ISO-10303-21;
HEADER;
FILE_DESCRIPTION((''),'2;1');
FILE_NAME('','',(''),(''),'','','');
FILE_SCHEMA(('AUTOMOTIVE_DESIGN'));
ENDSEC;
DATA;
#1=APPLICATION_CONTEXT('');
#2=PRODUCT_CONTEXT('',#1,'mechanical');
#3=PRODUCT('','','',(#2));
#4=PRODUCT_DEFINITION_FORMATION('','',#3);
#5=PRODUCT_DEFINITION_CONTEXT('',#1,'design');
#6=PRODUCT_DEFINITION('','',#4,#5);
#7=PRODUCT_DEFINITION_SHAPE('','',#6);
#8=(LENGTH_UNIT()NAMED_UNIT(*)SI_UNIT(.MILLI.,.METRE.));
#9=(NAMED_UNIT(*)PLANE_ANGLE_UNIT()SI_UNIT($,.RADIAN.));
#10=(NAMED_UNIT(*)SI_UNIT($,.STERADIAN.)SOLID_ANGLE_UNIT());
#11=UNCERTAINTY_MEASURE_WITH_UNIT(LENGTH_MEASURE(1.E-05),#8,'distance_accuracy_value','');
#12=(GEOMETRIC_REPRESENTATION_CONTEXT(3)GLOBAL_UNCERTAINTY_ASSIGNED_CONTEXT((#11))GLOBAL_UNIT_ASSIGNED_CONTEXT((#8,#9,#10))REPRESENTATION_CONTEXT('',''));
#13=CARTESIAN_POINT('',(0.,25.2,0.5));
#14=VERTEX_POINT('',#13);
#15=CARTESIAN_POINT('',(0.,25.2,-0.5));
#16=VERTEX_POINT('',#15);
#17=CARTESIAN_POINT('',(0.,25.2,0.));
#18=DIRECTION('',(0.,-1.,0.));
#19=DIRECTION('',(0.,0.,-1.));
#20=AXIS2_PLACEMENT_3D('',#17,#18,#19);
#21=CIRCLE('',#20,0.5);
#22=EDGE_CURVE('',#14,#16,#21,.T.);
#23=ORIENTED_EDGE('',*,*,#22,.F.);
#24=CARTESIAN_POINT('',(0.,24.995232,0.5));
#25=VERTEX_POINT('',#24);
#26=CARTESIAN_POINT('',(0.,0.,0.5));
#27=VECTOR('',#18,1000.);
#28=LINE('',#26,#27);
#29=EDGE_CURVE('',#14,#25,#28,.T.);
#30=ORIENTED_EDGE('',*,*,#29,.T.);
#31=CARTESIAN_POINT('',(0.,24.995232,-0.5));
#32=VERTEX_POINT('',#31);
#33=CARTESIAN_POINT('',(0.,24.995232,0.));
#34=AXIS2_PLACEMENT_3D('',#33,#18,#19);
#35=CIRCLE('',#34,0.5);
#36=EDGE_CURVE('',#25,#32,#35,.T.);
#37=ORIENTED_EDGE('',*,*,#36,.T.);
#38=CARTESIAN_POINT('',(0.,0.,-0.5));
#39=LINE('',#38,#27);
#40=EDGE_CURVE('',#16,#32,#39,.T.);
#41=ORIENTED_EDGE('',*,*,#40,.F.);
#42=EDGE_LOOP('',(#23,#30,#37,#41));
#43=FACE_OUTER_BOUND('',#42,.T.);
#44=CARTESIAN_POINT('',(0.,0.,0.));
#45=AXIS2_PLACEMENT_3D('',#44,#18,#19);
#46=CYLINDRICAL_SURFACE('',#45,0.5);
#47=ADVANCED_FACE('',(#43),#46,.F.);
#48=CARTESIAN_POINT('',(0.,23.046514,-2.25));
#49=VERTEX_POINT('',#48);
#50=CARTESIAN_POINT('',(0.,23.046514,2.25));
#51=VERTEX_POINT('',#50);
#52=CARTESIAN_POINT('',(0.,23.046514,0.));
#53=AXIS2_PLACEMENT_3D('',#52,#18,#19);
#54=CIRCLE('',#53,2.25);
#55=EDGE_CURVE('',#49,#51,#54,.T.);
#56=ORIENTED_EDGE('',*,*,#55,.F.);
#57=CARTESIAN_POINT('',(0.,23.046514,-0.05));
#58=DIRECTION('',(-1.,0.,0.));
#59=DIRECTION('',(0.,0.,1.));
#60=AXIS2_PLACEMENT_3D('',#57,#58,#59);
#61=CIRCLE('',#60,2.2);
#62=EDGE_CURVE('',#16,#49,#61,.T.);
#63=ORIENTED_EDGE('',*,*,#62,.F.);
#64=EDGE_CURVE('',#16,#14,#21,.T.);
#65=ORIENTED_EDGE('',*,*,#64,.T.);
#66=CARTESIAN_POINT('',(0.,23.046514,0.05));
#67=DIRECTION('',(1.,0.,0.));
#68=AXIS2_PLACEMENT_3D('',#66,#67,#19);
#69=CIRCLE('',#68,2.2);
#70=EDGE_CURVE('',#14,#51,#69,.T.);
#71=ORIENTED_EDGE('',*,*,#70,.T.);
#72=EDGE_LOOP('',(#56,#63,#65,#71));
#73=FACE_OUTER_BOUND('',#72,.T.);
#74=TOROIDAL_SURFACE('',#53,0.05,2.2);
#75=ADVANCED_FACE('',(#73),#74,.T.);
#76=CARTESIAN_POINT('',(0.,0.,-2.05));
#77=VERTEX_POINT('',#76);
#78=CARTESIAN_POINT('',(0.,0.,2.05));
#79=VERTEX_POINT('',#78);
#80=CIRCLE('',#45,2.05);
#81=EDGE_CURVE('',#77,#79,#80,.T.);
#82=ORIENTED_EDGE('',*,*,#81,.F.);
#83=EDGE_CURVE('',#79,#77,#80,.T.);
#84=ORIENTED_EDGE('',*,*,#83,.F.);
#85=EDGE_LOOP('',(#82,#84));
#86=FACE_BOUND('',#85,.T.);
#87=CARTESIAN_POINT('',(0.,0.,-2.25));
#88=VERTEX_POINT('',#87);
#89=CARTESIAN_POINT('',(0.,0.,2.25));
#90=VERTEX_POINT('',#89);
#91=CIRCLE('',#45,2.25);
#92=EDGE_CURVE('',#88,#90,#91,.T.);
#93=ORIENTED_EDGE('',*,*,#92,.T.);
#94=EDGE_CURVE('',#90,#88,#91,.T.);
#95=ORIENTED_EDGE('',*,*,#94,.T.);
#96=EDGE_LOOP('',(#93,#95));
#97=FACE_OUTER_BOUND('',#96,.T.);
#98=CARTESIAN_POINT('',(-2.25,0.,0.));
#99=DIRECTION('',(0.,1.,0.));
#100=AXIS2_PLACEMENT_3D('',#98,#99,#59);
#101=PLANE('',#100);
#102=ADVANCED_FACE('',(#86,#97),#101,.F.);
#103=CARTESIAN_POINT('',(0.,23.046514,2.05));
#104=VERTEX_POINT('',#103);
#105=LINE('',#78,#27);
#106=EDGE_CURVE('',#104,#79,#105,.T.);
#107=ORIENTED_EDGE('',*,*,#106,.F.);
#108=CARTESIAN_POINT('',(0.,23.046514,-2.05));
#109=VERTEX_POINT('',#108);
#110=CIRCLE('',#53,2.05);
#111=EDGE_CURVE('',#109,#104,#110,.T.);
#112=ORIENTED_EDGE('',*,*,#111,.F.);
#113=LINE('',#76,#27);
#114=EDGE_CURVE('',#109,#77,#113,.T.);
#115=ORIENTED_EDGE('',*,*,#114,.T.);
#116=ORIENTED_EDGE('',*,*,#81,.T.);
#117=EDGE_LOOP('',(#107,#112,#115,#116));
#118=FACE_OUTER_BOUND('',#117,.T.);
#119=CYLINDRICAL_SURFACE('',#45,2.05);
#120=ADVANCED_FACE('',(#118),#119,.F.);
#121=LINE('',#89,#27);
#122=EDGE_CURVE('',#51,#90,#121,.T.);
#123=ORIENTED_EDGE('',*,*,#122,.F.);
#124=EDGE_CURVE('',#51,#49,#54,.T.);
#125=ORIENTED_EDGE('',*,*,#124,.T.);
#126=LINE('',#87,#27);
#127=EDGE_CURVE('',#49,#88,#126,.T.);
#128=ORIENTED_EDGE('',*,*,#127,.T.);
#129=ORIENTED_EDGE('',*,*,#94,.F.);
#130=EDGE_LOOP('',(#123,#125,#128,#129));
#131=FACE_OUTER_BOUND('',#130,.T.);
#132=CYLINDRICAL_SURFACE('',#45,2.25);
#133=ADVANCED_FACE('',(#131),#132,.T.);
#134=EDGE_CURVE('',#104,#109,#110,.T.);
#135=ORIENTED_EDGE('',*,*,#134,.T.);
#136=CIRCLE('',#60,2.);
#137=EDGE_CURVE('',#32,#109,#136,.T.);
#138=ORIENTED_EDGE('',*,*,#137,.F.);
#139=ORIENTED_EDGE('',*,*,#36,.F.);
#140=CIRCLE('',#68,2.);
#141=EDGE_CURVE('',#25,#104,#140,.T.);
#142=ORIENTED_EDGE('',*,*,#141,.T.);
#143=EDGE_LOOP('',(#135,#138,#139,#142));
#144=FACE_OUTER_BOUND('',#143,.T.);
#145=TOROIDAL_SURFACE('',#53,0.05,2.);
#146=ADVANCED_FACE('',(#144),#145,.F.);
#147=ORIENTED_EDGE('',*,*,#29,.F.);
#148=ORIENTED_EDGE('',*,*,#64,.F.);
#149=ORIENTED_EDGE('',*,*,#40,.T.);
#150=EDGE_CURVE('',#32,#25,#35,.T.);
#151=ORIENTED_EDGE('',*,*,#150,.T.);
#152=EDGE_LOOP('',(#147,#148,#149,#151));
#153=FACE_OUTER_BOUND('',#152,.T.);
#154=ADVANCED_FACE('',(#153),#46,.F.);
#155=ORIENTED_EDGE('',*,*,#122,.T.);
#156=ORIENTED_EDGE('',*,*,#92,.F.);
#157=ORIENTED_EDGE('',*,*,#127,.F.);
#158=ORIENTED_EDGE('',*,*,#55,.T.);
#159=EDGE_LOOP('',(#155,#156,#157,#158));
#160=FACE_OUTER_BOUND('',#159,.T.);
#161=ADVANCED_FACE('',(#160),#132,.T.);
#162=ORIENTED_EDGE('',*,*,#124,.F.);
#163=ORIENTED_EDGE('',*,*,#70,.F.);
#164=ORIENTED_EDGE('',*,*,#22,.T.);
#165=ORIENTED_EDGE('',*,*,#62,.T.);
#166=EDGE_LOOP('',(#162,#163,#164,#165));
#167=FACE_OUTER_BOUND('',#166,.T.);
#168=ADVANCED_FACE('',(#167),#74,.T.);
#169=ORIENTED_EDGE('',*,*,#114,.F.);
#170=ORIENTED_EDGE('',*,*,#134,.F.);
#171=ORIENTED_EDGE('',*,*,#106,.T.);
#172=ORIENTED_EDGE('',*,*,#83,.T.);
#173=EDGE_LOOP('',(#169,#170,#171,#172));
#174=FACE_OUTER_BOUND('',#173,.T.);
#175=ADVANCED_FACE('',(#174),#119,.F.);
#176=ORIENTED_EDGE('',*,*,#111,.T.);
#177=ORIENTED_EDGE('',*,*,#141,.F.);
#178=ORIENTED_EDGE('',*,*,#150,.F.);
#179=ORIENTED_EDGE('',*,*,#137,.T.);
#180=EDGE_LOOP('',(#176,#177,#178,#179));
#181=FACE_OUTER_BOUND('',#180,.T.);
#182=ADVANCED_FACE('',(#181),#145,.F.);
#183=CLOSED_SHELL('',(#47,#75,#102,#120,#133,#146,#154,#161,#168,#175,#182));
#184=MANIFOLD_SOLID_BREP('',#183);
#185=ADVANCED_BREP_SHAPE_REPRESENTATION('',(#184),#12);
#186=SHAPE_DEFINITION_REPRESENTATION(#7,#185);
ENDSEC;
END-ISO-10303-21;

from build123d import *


with BuildPart() as part:
    # Sketch1 → Revolve1 (revolve)
    with BuildSketch(Plane.XY, mode=Mode.PRIVATE) as revolve1_sk:
        with BuildLine():
            Line((-2.25, 0), (-2.25, 23.046514453))
            ThreePointArc((-2.25, 23.046514453), (-1.757337108, 24.433958146), (-0.5, 25.2))
            Line((-0.5, 25.2), (-0.5, 24.99523198))
            ThreePointArc((-0.5, 24.99523198), (-1.615247584, 24.291504413), (-2.05, 23.046514453))
            Line((-2.05, 23.046514453), (-2.05, 0))
            Line((-2.05, 0), (-2.25, 0))
        make_face()
    revolve(revolve1_sk.sketch.rotate(Axis((0, 0, 0), (0, 1, 0)), 270), axis=Axis((0, 0, 0), (0, 1, 0)))


solid = part.part
